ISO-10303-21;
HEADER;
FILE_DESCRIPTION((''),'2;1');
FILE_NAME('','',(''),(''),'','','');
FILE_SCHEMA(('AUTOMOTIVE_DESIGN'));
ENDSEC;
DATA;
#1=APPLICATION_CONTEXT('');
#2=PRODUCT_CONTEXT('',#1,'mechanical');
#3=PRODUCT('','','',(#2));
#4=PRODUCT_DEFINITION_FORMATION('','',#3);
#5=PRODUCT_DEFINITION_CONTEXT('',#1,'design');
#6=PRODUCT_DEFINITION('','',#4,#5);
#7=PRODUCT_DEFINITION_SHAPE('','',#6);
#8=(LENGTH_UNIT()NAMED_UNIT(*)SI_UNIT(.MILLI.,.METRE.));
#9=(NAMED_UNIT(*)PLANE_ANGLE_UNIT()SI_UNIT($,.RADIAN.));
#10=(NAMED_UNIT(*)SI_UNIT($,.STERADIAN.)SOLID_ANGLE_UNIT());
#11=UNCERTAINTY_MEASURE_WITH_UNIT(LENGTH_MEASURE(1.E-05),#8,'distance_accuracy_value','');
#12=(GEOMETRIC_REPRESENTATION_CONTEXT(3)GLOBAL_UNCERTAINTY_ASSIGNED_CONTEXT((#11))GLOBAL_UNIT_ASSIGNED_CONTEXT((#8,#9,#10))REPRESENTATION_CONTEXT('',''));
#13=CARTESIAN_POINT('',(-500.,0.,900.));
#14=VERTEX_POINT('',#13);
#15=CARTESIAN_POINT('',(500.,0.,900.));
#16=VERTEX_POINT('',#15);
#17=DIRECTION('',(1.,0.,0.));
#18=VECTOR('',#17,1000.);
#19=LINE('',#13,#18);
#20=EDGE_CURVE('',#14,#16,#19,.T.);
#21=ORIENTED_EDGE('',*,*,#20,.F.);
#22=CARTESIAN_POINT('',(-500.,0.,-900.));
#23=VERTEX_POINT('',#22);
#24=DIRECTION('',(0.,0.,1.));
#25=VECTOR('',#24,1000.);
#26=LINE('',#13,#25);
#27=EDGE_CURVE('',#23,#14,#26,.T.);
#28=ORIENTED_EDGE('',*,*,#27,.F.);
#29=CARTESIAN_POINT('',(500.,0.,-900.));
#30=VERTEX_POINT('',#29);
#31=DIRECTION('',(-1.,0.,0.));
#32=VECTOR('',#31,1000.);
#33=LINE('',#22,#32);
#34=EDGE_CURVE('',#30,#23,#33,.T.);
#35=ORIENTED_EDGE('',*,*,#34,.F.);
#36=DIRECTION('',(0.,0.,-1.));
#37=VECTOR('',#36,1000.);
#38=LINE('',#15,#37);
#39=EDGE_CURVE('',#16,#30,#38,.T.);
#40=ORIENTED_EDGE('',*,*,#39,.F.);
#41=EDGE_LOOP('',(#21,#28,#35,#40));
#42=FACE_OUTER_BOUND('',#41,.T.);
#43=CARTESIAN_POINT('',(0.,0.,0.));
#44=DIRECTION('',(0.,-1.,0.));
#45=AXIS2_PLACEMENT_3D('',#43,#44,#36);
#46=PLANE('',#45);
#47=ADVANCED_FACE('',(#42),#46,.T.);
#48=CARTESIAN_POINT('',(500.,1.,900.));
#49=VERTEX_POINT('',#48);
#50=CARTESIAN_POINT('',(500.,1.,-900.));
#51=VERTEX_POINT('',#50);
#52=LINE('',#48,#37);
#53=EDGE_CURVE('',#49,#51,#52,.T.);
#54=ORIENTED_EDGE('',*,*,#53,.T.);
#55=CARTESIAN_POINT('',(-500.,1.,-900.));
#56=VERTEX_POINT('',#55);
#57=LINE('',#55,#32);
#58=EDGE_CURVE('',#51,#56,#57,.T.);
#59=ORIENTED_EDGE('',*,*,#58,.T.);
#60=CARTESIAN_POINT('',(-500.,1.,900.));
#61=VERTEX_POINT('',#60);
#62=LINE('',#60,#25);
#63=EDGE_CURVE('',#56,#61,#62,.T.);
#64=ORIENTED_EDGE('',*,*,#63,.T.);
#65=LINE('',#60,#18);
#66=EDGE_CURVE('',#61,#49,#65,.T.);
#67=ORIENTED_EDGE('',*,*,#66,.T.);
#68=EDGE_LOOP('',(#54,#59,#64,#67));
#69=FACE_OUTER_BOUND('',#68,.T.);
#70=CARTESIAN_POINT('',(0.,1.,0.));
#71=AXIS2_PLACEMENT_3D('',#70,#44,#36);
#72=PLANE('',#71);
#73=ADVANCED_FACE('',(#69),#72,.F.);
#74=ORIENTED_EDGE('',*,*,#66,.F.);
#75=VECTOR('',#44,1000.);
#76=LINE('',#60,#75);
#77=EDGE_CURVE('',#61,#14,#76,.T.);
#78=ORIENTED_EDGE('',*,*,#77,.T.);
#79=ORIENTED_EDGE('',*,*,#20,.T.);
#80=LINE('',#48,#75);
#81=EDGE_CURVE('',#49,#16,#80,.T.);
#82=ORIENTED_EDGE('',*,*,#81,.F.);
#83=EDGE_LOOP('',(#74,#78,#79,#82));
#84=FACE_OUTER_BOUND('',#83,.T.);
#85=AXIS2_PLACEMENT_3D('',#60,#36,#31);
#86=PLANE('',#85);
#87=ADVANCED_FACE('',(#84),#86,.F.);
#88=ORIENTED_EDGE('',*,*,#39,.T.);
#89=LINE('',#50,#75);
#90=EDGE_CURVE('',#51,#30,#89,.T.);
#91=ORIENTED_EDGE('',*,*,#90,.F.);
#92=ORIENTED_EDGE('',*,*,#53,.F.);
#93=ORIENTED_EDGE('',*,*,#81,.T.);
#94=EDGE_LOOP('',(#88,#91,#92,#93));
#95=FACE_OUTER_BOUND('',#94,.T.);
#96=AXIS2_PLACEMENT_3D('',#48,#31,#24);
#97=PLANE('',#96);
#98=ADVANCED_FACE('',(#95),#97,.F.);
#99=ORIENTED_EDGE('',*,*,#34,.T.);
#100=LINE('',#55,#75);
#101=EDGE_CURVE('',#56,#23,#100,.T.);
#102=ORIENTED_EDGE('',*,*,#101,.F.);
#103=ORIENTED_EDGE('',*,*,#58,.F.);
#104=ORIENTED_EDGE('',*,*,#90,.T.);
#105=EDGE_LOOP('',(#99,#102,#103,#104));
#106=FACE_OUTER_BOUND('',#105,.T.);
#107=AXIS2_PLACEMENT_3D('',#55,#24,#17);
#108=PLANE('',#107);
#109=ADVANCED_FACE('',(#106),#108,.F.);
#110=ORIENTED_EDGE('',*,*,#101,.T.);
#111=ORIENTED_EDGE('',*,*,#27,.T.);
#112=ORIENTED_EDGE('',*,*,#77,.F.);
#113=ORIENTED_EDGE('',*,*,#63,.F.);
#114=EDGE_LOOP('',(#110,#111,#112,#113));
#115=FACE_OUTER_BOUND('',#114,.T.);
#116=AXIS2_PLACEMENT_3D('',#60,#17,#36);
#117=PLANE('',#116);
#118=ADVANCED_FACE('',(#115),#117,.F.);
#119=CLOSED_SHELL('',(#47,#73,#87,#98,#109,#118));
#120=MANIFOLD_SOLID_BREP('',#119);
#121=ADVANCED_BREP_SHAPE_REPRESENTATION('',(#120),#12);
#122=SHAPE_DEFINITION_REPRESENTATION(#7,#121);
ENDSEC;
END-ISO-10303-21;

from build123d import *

# Parameters (mm, degrees)
SKETCH1_W           = 1000
SKETCH1_H           = 1800
BOSS_EXTRUDE1_DEPTH = 1


with BuildPart() as part:
    # Sketch1 → Boss-Extrude1 (new body)
    with BuildSketch(Plane(origin=(0, 0, 0), x_dir=(1, 0, 0), z_dir=(0, 1, 0))):
        Rectangle(SKETCH1_W, SKETCH1_H)
    extrude(amount=BOSS_EXTRUDE1_DEPTH)


solid = part.part
